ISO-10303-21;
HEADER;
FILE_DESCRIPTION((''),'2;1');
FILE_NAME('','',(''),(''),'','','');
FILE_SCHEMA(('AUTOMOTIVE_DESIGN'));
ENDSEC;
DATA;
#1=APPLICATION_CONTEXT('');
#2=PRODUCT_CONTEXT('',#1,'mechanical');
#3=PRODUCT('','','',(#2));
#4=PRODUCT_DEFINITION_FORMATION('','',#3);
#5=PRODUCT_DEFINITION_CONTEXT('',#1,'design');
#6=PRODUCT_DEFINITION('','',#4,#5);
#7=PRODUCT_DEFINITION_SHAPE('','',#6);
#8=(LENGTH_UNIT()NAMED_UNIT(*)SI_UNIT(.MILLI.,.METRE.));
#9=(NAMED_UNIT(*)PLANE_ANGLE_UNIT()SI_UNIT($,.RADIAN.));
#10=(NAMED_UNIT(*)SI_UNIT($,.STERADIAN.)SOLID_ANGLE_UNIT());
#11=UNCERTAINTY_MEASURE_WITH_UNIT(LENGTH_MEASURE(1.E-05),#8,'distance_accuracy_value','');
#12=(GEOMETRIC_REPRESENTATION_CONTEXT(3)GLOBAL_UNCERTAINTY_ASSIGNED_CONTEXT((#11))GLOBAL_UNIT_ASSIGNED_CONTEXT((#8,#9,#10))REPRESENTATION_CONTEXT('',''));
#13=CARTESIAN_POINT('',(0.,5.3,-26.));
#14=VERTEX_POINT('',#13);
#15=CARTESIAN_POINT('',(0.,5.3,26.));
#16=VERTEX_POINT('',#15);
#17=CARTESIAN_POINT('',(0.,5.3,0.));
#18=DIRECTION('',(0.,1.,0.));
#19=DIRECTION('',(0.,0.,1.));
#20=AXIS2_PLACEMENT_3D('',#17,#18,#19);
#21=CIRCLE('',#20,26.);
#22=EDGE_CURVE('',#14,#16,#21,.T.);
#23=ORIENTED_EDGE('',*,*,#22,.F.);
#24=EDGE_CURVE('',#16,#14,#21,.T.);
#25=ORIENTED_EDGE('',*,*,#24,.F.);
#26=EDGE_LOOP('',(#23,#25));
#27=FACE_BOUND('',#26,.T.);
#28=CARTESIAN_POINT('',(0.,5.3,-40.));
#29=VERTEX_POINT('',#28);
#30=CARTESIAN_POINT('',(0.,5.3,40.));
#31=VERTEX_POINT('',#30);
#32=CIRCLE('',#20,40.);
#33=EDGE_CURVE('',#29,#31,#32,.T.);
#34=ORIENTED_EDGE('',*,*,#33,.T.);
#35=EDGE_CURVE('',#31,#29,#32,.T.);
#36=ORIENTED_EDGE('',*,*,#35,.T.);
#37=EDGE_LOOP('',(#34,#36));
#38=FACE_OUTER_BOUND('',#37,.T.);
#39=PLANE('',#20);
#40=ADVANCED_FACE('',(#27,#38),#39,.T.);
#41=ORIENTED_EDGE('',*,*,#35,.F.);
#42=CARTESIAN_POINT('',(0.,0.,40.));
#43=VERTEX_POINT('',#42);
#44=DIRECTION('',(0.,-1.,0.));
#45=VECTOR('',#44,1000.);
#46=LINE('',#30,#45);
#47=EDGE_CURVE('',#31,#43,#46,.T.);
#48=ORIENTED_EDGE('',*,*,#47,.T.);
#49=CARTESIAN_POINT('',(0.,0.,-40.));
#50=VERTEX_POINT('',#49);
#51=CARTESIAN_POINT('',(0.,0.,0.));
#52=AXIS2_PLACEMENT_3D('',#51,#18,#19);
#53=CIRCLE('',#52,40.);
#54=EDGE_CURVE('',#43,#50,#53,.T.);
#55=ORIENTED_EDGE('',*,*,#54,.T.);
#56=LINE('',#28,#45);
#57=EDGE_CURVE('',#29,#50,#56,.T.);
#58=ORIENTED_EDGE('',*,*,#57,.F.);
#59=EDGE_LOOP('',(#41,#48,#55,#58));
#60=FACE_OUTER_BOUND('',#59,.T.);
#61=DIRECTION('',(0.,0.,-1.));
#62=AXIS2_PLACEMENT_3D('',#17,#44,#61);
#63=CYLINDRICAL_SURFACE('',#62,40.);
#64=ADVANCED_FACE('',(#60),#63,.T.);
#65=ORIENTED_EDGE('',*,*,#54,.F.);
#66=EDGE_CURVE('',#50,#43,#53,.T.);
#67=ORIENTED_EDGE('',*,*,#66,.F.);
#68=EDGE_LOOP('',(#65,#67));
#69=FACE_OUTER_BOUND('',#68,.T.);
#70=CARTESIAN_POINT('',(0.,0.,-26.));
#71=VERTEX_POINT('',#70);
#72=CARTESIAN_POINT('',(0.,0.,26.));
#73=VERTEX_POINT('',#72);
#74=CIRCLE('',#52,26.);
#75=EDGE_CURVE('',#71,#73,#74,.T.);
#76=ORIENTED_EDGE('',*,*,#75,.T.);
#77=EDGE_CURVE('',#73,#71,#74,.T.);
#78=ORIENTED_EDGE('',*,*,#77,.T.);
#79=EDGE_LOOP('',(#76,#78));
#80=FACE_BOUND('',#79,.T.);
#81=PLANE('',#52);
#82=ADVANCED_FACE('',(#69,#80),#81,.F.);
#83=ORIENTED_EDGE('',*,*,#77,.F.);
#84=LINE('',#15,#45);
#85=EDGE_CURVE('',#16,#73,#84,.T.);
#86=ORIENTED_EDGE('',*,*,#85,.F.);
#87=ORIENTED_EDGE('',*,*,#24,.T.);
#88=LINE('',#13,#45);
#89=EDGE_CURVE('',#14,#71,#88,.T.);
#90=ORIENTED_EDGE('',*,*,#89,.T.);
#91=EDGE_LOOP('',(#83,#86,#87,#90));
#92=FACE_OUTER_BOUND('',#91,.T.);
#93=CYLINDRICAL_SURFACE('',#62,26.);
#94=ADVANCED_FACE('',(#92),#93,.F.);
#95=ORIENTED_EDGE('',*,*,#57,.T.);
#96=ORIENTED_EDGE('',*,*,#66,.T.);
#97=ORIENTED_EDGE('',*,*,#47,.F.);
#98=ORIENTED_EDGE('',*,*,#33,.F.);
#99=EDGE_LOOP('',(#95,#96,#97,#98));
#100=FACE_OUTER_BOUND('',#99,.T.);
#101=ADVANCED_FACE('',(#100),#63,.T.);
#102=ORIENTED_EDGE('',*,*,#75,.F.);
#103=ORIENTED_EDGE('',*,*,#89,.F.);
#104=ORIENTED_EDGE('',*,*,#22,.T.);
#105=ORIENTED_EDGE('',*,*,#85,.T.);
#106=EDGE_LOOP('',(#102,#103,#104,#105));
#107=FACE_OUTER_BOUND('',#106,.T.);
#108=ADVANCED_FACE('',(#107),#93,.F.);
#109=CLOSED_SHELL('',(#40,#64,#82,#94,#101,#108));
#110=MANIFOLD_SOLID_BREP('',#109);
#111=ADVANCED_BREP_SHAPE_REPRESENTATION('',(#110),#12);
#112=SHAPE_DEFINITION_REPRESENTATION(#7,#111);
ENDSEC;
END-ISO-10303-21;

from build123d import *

# Parameters (mm, degrees)
SKETCH1_R           = 40
SKETCH1_R_2         = 26
BOSS_EXTRUDE1_DEPTH = 5.3


with BuildPart() as part:
    # Sketch1 → Boss-Extrude1 (new body)
    with BuildSketch(Plane(origin=(0, 0, 0), x_dir=(1, 0, 0), z_dir=(0, 1, 0))):
        with Locations(Location((0, 0, 0), (0, 0, 270))):
            Circle(SKETCH1_R)
        with Locations(Location((0, 0, 0), (0, 0, 270))):
            Circle(SKETCH1_R_2, mode=Mode.SUBTRACT)
    extrude(amount=BOSS_EXTRUDE1_DEPTH)


solid = part.part
